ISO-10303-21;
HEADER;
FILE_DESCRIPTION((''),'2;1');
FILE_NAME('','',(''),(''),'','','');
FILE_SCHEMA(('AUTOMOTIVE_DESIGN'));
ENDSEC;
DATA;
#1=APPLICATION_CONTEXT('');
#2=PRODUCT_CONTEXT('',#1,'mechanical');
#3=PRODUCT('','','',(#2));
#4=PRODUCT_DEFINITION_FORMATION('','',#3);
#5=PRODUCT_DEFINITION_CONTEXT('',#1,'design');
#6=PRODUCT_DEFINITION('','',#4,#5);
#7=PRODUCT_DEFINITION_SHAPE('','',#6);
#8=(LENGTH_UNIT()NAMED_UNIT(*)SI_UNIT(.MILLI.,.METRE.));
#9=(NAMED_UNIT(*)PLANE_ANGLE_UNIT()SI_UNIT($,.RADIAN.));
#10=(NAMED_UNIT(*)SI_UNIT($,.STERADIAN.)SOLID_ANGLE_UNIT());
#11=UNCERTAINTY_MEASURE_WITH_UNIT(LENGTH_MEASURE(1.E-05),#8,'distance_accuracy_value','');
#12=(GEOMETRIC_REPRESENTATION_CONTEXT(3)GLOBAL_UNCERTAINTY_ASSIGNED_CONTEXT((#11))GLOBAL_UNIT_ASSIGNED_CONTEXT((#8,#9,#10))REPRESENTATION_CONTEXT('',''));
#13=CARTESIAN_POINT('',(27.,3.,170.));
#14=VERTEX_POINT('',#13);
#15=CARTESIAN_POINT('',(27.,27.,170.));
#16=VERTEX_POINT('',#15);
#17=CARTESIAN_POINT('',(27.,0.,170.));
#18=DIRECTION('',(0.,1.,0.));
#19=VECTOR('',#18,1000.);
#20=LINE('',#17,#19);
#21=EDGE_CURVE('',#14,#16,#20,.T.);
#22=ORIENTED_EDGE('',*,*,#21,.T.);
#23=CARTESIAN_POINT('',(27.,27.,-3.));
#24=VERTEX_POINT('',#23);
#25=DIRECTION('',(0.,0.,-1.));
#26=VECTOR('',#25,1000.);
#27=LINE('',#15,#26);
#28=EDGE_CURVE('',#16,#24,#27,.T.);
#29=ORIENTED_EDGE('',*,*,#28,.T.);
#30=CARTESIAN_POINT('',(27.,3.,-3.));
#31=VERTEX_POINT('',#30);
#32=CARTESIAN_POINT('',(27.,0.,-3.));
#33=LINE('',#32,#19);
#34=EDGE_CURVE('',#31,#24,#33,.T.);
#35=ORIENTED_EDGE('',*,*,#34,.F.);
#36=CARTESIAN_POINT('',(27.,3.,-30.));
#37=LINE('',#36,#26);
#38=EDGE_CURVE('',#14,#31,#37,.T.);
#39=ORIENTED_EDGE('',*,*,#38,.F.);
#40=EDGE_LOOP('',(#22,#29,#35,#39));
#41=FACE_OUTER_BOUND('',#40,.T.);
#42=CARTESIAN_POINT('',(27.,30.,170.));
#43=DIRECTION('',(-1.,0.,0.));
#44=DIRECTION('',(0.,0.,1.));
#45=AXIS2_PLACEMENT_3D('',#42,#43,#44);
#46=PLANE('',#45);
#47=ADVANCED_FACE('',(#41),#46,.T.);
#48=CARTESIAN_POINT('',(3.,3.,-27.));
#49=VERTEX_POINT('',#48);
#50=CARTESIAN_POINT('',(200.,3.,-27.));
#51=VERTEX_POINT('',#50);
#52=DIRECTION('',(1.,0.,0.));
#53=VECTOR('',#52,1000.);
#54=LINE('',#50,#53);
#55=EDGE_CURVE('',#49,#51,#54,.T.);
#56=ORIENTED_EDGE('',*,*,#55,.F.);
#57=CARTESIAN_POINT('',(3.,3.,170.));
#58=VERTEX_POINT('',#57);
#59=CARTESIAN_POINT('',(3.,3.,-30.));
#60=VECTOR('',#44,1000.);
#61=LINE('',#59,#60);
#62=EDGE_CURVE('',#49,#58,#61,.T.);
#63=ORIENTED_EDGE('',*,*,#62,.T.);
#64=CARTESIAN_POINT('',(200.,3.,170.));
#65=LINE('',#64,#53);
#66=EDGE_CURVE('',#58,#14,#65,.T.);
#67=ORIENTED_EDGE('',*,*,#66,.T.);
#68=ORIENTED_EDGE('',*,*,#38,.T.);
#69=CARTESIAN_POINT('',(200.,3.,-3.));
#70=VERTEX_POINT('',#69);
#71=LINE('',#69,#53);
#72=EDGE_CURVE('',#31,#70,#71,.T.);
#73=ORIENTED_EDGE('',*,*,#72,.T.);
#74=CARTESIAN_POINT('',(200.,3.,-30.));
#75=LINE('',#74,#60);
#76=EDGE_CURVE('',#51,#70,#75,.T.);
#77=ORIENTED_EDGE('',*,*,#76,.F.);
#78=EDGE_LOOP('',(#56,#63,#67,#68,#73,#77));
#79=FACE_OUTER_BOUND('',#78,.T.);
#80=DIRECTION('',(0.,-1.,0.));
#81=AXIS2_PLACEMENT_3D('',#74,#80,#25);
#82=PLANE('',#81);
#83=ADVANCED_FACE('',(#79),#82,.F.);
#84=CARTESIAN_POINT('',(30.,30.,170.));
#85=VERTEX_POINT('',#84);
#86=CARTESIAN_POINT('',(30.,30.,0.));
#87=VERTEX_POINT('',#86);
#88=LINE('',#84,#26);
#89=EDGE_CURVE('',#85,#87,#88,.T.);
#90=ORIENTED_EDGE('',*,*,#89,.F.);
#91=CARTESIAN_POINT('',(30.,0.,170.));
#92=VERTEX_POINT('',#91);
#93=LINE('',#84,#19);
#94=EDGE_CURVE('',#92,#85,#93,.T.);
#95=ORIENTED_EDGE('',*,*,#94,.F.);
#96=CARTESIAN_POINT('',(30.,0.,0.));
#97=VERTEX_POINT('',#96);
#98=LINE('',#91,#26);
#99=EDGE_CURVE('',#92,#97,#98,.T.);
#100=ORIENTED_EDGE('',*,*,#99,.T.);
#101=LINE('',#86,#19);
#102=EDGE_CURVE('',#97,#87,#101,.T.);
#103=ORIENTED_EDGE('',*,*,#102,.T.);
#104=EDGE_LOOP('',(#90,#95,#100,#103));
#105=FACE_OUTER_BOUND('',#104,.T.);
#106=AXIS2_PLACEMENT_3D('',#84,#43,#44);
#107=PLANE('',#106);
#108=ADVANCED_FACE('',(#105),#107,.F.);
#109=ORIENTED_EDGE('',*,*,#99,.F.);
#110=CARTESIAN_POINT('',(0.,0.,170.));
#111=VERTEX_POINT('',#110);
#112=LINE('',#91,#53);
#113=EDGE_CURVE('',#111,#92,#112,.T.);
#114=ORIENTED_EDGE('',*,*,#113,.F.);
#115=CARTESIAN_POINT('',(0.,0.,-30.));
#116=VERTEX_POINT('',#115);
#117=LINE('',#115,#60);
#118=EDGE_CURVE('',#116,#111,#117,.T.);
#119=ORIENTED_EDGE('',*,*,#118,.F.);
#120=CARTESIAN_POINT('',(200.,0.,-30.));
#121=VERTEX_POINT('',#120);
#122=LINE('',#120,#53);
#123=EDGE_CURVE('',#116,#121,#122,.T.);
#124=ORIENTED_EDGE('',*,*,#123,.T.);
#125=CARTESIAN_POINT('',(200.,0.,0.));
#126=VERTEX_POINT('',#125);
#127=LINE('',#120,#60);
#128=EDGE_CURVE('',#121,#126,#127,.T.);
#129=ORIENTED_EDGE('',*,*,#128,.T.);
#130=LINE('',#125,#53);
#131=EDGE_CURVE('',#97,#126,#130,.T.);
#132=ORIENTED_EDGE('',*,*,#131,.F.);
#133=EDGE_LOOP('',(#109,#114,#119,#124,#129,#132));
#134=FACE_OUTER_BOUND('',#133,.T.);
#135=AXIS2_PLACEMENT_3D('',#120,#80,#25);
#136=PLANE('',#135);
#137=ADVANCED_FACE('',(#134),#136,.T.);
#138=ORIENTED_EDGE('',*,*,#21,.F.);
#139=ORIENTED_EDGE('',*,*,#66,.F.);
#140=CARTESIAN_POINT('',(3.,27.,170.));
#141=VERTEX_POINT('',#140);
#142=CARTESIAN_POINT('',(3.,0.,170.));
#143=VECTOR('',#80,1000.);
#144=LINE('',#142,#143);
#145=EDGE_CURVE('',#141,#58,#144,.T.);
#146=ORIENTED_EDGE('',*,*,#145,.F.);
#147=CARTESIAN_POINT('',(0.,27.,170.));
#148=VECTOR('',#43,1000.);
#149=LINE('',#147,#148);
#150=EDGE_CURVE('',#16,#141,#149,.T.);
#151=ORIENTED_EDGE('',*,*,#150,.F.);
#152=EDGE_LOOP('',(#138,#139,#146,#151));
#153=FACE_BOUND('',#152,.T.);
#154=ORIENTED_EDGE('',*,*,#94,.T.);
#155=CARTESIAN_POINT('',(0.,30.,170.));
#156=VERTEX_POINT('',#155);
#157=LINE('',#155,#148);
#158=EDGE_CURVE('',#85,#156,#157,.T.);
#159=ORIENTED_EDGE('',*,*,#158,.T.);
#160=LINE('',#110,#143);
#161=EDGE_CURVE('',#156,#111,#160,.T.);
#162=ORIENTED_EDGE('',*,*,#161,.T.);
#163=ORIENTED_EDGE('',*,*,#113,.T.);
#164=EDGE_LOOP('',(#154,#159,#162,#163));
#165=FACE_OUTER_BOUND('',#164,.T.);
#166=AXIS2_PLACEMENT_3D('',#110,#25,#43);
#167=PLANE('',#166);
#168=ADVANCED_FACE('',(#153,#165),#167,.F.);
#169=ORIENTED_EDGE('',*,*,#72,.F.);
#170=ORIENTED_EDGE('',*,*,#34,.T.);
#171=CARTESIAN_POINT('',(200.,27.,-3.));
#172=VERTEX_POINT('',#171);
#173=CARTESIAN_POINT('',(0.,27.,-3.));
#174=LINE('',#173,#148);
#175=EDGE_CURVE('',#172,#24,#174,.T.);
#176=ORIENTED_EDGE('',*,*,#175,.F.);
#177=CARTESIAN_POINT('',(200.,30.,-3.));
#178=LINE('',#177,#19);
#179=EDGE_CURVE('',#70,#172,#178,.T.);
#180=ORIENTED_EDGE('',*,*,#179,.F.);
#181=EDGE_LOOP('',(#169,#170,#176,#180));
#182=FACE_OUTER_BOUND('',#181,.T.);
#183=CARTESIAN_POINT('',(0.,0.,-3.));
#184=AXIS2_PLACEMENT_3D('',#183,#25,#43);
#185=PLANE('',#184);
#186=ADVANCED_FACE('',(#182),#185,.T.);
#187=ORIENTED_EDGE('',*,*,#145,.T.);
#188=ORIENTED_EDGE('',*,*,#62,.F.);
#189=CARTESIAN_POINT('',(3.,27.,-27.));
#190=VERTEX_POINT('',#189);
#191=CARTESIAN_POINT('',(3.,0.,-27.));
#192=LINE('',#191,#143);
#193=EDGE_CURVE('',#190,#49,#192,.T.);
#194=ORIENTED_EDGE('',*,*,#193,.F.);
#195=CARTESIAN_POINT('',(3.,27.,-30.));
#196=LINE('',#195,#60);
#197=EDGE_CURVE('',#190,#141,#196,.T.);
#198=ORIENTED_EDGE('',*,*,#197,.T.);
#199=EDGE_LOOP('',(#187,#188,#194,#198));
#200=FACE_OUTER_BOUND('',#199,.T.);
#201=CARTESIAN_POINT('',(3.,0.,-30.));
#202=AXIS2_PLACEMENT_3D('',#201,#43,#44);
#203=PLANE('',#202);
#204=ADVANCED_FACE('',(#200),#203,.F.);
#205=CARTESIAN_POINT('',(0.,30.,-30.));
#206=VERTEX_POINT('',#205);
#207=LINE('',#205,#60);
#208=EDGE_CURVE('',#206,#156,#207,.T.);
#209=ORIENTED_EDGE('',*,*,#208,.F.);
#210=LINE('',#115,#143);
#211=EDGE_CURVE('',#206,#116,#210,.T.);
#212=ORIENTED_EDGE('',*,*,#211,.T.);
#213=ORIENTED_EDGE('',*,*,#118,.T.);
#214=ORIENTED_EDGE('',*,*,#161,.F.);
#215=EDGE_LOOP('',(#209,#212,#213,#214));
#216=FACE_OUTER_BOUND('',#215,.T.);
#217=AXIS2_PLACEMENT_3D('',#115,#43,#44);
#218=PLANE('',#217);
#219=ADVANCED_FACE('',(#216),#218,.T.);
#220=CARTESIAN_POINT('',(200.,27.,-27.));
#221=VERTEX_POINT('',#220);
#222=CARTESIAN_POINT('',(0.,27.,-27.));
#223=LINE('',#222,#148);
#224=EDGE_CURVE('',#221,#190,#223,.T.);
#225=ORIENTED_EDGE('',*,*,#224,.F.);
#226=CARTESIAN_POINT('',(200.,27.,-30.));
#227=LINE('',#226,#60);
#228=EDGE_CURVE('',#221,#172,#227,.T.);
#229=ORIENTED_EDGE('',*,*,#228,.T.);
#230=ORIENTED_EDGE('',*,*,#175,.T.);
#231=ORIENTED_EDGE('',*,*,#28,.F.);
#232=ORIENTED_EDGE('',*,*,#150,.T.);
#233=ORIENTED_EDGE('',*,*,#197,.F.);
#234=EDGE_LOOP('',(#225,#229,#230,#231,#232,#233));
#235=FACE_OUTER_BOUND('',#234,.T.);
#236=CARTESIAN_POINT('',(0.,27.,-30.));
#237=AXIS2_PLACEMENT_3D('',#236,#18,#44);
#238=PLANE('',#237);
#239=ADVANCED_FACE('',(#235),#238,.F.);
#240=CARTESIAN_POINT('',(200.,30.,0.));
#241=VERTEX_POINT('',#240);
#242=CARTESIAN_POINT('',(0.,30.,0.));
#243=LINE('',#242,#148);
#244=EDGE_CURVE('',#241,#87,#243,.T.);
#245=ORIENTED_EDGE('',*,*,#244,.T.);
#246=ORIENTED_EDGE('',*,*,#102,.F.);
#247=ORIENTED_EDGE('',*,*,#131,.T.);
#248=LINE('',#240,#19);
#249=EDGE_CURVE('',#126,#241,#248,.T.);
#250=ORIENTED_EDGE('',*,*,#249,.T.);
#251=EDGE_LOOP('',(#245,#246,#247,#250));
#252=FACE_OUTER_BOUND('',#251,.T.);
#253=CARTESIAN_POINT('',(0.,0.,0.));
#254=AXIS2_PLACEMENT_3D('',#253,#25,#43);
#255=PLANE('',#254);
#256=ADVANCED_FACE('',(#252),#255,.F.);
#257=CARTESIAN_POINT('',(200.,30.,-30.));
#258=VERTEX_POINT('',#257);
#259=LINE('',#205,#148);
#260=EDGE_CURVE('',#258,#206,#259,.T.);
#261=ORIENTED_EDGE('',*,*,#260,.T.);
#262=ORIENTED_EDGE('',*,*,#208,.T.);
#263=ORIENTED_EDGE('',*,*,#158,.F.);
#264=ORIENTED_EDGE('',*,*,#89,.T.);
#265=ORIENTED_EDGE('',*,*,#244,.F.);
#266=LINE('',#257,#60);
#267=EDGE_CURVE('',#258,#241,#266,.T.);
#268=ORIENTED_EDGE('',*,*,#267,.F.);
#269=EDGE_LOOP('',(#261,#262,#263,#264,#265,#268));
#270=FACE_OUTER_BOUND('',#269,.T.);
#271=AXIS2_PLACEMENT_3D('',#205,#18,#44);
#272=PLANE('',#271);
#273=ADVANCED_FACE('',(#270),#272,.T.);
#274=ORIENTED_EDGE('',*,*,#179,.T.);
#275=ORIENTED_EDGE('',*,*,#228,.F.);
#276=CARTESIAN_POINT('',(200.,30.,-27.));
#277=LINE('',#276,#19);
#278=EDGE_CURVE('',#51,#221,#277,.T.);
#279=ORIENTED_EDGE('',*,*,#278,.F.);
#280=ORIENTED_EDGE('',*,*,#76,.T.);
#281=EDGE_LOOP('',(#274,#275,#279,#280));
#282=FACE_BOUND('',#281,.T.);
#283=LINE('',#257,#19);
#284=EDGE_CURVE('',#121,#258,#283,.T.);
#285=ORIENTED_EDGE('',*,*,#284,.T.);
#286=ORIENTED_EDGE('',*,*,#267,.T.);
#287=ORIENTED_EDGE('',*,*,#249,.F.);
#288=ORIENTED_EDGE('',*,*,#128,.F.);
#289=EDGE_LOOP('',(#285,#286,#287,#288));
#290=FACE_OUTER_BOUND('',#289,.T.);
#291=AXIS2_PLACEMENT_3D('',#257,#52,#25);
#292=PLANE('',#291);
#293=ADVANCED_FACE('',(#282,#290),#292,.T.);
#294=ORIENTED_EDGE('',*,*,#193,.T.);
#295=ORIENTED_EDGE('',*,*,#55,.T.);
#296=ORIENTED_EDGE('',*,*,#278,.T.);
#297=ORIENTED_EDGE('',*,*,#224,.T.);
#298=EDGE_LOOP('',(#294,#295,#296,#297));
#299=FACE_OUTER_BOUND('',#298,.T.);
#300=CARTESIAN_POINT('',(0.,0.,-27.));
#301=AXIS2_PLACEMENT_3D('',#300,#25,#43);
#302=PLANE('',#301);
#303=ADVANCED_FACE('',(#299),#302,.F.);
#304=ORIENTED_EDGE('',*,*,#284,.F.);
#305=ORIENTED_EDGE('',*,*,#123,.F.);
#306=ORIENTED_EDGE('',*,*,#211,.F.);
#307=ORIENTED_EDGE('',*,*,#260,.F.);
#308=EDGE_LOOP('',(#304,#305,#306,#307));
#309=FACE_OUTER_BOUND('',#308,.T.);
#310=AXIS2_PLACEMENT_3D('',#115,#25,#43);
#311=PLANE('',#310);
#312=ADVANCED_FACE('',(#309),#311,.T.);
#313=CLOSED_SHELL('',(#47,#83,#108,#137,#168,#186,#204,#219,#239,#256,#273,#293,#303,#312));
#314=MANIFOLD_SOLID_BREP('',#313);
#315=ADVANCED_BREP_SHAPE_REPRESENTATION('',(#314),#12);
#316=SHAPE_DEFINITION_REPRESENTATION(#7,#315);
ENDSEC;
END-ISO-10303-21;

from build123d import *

# Parameters (mm, degrees)
SKETCH_1_W      = 200
SKETCH_1_H      = 30
EXTRUDE_1_DEPTH = 30
SKETCH_2_W      = 30
SKETCH_2_H      = 30
EXTRUDE_2_DEPTH = 170
SHELL_1_T       = -3


with BuildPart() as part:
    # 草图1 → 凸台-拉伸1 (new body)
    with BuildSketch(Plane.XY):
        with Locations((100, 15)):
            Rectangle(SKETCH_1_W, SKETCH_1_H)
    extrude(amount=-EXTRUDE_1_DEPTH)

    # 草图2 → 凸台-拉伸2 (add)
    with BuildSketch(Plane.XY):
        with Locations((15, 15)):
            Rectangle(SKETCH_2_W, SKETCH_2_H)
    extrude(amount=EXTRUDE_2_DEPTH)

    # 抽壳1
    shell_1_openings = [part.faces().sort_by_distance(p)[0] for p in [
        (15, 15, 170),
        (200, 15, -15),
    ]]
    offset(amount=SHELL_1_T, openings=shell_1_openings, kind=Kind.INTERSECTION)


solid = part.part
